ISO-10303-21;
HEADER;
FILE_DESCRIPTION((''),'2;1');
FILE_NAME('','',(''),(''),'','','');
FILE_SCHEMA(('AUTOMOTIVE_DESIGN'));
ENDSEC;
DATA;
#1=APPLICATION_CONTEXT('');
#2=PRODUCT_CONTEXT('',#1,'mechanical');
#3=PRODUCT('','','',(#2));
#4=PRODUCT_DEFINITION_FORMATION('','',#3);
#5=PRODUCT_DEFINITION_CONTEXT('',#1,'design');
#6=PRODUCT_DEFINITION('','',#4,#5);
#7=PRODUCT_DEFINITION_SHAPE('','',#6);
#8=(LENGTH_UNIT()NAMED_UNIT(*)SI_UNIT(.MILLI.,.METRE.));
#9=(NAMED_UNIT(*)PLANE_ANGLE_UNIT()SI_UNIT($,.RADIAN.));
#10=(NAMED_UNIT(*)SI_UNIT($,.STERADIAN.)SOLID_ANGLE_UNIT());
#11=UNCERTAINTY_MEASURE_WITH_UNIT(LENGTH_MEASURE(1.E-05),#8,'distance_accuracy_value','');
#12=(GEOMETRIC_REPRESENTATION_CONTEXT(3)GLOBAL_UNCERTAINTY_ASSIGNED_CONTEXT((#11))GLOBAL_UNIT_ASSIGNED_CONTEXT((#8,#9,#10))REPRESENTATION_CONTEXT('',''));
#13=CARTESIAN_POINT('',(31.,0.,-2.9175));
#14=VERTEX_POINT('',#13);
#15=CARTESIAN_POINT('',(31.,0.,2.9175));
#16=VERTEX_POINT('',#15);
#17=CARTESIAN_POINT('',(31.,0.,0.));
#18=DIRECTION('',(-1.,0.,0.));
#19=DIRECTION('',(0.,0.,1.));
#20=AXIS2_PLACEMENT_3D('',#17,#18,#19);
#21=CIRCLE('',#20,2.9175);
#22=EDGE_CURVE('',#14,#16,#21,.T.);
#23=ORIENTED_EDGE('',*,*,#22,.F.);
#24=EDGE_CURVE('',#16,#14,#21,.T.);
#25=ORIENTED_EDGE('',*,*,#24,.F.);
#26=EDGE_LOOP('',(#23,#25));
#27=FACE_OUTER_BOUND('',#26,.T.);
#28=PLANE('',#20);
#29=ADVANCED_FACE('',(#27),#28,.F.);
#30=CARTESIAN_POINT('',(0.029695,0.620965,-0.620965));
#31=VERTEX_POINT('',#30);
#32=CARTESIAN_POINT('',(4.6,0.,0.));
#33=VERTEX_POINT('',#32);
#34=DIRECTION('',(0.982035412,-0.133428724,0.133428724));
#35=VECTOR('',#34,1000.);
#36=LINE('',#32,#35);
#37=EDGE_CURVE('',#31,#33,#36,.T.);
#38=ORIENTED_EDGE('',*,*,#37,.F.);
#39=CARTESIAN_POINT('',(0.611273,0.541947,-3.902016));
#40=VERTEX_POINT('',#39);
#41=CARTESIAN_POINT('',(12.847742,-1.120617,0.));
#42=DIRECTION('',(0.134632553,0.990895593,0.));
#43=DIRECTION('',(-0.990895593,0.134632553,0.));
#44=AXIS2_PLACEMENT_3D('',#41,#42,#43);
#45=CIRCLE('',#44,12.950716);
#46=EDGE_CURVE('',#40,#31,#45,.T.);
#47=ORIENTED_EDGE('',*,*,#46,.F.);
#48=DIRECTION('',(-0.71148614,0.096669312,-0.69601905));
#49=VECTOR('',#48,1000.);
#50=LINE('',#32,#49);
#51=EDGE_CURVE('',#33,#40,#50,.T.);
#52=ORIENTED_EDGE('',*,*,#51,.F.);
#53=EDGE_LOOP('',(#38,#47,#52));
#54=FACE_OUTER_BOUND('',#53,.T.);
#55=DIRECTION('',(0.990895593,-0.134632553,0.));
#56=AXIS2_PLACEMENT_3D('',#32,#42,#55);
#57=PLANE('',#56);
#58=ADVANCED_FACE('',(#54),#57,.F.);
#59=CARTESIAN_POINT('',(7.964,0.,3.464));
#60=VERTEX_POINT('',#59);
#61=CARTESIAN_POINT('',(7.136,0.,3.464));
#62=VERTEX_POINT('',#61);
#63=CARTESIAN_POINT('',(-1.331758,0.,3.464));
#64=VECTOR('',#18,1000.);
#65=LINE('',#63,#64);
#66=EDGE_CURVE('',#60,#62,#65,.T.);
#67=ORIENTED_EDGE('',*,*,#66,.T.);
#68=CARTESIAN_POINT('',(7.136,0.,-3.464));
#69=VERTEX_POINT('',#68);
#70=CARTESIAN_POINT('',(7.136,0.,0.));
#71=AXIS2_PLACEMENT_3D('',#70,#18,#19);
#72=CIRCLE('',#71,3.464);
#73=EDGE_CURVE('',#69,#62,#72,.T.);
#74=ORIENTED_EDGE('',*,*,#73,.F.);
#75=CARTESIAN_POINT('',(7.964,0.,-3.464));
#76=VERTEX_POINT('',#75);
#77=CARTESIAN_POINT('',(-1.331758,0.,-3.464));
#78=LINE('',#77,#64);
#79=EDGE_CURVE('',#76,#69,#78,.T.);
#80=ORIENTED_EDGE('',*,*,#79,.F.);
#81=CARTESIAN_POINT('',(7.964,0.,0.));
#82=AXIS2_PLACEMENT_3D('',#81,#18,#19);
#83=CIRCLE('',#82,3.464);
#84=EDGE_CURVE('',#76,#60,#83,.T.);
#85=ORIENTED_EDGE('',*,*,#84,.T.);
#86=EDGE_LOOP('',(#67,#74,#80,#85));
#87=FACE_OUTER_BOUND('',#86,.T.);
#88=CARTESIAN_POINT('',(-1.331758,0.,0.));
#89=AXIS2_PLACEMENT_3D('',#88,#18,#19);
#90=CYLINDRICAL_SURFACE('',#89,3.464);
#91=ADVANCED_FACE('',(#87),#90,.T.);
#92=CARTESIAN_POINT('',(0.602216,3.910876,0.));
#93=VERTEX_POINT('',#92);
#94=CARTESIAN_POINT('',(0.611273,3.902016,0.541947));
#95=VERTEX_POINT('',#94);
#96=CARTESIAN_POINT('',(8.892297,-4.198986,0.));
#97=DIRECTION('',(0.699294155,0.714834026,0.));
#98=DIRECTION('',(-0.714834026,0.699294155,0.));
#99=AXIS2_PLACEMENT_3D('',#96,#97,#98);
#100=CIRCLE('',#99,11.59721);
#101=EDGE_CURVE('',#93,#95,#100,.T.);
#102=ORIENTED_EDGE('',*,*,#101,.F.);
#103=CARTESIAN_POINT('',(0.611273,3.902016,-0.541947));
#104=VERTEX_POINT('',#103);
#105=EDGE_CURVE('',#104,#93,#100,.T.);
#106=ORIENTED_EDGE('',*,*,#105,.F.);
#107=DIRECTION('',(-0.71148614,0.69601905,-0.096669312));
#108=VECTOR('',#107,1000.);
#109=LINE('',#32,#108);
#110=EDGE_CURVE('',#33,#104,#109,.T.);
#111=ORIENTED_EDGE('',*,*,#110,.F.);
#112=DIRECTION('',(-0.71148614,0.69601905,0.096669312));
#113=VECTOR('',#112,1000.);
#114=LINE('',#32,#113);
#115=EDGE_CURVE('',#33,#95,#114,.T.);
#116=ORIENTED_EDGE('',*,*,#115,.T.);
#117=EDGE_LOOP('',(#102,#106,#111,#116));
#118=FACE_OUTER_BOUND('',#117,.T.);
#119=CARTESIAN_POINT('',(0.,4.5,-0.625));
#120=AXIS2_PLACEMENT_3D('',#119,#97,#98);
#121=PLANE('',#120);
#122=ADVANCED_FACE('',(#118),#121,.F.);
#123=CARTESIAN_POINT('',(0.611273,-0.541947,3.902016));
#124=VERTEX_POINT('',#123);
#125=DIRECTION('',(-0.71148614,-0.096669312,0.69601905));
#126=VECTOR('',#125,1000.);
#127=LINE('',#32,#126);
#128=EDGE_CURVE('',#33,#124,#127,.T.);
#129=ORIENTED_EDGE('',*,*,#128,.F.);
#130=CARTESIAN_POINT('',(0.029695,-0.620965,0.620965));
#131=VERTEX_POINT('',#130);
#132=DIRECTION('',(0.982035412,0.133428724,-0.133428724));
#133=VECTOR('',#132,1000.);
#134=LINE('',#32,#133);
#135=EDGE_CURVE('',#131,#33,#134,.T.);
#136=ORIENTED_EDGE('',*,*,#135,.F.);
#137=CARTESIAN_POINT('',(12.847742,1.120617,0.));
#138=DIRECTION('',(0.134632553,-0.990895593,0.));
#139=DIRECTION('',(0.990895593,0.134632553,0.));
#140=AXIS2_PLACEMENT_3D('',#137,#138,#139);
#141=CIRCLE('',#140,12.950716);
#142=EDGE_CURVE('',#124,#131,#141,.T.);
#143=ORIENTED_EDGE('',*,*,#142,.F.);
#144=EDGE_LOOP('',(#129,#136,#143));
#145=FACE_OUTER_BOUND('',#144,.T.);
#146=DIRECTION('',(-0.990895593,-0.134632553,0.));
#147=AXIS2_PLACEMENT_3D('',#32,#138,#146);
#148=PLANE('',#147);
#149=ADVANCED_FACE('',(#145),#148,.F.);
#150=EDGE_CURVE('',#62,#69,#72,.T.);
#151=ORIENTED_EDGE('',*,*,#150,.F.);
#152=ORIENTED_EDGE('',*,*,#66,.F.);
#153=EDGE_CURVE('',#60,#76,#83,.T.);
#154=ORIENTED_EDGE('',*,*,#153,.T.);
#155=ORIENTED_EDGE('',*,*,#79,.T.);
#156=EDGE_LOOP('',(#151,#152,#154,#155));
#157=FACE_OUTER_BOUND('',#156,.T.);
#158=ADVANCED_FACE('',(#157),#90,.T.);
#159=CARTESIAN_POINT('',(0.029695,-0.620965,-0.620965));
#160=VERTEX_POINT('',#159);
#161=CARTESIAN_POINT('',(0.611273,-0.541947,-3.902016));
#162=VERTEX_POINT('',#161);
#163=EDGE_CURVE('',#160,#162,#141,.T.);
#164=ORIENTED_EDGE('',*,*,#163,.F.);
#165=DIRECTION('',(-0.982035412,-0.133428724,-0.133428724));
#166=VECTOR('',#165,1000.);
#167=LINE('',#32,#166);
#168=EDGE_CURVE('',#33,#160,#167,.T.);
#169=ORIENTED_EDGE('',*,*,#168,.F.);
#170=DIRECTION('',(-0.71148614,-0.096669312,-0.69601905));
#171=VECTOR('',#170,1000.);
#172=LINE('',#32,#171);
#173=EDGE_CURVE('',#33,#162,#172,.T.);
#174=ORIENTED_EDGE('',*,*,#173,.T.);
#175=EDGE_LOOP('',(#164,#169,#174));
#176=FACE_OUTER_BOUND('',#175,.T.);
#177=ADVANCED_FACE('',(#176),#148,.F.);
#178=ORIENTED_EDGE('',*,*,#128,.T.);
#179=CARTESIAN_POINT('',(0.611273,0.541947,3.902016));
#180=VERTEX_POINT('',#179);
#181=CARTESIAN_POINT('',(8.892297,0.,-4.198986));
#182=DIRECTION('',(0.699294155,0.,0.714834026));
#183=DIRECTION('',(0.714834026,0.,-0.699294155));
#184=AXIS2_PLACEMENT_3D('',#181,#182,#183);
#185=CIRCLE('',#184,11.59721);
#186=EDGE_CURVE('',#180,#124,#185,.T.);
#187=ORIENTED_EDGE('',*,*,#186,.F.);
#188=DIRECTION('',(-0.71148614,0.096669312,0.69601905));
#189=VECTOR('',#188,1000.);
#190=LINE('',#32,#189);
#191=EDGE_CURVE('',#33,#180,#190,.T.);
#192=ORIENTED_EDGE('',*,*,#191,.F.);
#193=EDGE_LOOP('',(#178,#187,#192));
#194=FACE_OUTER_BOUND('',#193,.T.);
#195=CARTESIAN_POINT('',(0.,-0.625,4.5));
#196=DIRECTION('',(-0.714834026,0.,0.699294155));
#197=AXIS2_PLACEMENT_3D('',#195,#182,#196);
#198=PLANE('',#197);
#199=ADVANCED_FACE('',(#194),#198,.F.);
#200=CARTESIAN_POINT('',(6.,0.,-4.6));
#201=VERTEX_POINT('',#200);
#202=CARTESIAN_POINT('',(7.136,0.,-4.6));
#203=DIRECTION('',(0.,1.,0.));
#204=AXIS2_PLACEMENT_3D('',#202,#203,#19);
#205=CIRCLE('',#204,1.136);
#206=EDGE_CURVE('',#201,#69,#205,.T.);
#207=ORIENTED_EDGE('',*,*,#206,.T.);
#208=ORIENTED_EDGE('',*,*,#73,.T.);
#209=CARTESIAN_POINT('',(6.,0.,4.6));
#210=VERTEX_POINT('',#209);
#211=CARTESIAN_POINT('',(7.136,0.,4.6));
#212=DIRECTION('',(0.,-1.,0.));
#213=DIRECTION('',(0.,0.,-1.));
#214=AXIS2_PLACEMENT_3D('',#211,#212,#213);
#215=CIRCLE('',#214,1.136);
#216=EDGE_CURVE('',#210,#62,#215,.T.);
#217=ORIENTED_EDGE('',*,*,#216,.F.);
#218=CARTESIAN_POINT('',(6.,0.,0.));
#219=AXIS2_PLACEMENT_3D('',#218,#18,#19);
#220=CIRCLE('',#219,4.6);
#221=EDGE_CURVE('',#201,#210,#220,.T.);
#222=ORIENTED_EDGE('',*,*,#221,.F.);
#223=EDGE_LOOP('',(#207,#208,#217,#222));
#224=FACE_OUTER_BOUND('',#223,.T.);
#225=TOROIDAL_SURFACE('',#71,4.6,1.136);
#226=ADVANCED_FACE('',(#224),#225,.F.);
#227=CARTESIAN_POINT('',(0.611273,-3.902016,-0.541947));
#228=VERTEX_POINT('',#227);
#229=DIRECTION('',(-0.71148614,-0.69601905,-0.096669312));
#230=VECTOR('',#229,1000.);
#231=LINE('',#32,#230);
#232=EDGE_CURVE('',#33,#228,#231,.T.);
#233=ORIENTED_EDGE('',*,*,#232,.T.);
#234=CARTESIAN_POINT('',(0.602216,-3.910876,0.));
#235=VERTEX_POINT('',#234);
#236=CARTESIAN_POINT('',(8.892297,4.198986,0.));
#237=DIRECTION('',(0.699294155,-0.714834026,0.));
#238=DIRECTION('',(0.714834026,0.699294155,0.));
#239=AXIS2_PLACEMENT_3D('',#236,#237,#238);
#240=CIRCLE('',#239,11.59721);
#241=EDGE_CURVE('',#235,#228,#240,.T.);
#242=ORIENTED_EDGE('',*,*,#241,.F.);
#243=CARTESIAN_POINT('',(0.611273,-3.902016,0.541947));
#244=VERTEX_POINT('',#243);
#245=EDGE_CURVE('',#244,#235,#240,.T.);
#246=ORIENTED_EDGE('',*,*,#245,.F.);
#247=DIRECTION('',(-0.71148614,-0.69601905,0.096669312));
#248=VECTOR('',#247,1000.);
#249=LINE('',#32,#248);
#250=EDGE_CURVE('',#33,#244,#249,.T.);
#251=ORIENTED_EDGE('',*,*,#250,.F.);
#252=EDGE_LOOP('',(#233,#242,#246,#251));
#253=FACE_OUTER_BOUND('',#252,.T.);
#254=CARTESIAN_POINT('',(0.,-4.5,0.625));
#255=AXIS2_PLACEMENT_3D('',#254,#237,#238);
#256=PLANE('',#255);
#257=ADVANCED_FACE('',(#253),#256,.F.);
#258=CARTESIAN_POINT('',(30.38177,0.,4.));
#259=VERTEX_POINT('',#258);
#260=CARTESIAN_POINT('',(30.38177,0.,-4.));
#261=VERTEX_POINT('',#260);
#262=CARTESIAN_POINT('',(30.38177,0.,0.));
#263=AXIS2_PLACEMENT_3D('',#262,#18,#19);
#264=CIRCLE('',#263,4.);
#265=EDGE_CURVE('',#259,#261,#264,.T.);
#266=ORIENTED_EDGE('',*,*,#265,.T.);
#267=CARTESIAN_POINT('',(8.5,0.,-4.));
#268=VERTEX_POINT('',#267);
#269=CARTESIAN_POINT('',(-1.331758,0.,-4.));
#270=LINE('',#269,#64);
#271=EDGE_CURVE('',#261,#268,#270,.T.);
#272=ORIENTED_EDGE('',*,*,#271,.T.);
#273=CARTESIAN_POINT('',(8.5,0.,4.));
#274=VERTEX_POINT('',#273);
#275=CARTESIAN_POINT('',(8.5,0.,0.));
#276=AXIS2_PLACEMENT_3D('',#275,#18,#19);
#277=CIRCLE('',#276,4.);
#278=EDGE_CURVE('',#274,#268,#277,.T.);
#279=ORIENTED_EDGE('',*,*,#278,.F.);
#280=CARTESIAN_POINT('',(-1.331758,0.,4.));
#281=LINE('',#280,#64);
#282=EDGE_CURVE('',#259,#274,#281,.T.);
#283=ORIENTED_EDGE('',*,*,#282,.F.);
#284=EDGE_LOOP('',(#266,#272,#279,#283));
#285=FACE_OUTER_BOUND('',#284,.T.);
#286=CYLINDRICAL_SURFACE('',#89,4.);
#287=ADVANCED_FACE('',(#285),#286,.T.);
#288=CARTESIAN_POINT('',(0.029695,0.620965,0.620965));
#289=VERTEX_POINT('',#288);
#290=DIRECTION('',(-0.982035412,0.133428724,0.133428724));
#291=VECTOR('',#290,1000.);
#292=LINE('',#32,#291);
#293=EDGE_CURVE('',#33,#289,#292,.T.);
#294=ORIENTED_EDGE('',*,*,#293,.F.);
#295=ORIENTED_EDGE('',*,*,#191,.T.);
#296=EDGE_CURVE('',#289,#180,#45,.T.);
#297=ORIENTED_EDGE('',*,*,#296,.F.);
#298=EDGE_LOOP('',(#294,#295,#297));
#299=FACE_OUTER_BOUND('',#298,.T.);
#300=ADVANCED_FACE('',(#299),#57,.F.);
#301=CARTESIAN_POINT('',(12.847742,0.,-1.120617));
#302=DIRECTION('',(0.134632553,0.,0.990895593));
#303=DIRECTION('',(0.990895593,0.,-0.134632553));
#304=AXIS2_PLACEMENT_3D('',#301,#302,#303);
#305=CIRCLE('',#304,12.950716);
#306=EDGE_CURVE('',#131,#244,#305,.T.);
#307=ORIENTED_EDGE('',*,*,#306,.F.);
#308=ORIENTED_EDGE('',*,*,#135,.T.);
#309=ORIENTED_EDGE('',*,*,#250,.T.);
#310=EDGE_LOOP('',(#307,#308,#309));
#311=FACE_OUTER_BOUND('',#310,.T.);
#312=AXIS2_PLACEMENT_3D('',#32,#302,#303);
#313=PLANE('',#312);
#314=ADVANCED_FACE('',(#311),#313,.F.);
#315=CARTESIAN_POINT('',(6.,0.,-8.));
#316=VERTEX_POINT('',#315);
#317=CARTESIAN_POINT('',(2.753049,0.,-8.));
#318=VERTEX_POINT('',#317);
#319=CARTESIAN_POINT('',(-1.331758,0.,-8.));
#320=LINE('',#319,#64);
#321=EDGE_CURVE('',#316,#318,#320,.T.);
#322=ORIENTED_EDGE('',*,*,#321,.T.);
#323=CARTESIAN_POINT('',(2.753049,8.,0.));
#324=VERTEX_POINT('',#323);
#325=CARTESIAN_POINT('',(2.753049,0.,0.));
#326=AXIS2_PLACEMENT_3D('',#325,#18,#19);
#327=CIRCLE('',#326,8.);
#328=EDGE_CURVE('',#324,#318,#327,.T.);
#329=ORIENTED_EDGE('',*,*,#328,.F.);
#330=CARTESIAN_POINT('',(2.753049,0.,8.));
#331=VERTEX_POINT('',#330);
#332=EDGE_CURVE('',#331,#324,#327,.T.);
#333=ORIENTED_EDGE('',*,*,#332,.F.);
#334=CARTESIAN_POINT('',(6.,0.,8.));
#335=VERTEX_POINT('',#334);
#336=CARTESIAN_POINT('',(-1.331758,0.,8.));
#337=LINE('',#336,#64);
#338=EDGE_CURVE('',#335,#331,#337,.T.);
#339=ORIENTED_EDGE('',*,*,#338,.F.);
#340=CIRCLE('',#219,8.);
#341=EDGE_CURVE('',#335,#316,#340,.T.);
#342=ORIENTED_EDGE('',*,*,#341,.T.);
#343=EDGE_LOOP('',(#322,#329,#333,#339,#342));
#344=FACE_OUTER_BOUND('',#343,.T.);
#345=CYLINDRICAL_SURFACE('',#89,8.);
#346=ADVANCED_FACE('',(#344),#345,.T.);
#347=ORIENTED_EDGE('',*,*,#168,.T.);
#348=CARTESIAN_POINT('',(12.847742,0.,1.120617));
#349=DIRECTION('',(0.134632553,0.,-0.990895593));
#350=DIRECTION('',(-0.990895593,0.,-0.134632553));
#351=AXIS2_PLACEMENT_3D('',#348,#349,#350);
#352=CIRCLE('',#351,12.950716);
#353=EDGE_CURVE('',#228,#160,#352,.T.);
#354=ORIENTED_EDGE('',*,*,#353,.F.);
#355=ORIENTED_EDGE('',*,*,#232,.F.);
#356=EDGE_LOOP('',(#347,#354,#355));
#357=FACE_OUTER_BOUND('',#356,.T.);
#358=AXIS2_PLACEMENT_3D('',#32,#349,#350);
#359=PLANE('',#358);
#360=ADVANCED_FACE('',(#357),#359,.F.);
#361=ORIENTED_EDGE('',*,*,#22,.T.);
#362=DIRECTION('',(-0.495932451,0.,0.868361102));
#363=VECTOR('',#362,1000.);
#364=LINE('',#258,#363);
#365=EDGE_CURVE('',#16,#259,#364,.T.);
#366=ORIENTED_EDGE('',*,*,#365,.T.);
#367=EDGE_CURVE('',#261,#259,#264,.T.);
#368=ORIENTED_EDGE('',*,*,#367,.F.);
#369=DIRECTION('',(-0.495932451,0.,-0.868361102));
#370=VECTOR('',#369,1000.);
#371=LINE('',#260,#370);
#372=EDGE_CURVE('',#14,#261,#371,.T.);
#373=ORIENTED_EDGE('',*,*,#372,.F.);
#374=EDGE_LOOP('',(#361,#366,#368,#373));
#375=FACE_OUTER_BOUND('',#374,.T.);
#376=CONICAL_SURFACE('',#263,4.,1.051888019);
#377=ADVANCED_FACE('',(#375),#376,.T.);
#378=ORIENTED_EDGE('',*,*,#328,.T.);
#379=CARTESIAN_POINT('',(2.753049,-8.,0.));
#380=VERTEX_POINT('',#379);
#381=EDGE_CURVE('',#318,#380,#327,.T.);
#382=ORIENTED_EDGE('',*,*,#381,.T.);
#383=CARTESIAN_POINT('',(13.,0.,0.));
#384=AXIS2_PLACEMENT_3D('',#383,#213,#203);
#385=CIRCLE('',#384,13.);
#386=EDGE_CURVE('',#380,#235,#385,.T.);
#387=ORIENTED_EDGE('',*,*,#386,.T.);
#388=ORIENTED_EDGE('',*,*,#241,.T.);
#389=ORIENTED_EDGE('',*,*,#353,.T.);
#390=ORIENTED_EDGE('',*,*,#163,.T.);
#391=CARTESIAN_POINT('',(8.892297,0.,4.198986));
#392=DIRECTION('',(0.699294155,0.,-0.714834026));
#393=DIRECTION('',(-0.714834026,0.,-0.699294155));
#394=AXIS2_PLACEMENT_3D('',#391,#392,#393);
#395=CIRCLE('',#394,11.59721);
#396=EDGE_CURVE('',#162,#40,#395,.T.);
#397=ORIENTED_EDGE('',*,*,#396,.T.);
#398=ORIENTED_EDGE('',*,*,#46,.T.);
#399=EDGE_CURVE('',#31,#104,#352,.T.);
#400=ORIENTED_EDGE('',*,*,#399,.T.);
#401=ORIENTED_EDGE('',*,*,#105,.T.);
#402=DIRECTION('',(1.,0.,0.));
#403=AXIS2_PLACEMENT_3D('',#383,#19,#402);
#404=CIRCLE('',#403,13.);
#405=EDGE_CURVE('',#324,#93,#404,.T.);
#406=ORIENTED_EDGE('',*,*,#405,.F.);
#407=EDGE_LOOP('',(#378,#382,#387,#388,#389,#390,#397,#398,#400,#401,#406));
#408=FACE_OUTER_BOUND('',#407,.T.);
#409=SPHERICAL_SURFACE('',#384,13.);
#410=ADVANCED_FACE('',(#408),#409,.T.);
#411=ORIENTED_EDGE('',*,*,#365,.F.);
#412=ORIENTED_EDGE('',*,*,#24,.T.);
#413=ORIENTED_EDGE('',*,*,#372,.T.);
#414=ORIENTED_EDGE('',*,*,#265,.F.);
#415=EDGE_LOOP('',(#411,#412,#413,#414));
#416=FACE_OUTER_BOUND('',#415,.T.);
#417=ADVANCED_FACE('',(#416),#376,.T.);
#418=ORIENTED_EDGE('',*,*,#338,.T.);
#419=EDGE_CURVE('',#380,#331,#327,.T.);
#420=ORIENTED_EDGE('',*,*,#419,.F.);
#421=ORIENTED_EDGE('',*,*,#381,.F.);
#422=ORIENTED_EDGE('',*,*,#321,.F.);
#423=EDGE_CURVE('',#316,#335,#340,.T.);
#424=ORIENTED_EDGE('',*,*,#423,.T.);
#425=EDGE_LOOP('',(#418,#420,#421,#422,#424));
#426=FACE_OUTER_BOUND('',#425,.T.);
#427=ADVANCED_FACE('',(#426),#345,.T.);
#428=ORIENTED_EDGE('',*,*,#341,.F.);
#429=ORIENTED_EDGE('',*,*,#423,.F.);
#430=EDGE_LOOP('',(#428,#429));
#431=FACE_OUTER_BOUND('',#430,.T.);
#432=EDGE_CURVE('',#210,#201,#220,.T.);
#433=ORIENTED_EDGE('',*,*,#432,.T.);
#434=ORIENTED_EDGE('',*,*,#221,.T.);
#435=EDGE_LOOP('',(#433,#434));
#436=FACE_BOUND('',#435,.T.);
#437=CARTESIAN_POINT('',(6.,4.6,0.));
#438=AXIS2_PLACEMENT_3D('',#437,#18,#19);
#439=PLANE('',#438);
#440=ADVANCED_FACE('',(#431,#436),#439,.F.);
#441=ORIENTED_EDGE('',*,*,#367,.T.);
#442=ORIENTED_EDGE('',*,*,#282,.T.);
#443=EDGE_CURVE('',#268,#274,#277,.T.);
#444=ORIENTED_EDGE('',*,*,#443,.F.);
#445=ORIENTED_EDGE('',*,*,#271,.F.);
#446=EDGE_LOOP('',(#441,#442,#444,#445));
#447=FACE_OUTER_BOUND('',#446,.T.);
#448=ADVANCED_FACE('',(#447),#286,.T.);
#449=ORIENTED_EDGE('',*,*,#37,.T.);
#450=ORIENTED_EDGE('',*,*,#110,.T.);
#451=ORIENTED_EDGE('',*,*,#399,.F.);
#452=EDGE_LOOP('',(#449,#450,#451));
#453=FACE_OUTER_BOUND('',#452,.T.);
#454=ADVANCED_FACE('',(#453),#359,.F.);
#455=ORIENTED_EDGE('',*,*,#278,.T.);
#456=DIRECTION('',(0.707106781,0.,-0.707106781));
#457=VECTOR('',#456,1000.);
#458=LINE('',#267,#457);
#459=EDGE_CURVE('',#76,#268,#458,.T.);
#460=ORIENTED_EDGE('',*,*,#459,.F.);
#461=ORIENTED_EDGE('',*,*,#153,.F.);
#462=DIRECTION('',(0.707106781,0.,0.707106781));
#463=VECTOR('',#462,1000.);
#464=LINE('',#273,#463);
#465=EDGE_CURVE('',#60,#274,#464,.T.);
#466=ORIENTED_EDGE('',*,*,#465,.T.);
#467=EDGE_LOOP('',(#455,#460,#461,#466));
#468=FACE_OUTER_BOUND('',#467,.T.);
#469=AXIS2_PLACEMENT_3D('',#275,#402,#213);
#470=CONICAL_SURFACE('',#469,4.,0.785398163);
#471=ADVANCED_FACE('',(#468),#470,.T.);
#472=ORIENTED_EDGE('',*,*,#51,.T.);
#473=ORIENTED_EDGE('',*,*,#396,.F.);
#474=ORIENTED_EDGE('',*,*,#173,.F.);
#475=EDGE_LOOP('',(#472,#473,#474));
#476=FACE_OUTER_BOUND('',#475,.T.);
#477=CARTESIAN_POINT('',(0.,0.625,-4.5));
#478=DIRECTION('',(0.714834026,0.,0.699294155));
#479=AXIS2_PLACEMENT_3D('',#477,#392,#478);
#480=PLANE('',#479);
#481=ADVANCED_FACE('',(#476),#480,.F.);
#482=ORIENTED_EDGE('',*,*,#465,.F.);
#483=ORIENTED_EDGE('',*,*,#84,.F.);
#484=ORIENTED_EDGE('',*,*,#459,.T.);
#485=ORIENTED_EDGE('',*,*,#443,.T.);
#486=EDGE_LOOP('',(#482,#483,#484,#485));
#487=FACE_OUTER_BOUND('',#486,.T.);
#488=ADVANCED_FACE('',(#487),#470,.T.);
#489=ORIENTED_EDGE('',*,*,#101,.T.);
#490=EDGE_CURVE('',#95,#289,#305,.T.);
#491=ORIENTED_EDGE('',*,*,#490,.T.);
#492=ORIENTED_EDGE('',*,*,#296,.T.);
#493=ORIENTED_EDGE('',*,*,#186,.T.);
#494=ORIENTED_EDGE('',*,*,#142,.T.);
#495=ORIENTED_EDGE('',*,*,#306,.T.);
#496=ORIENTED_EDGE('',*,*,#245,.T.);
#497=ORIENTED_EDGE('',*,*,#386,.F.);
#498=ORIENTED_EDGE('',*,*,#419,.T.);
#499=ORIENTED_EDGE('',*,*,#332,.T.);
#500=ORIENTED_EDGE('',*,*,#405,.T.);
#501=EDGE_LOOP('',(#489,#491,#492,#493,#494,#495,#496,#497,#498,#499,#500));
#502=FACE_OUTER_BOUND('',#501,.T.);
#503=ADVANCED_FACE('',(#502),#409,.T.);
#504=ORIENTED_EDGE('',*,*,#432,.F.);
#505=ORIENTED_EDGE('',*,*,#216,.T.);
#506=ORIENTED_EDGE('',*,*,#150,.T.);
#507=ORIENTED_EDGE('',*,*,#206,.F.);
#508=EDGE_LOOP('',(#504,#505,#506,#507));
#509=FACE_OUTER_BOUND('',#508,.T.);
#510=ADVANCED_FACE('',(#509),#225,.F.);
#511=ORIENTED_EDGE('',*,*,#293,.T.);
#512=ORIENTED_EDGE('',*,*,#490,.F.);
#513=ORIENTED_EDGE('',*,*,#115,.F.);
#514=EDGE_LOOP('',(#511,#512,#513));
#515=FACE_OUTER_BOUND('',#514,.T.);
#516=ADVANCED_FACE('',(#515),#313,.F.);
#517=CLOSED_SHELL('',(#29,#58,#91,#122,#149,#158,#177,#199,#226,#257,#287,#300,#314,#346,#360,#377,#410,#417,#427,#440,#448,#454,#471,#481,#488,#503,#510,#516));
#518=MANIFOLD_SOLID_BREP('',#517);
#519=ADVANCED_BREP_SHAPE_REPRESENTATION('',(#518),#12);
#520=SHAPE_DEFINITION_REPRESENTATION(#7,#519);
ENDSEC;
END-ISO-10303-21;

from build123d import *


with BuildPart() as part:
    # 草图2 → Revolve 709 (revolve)
    with BuildSketch(Plane.XY, mode=Mode.PRIVATE) as revolve_709_sk:
        with BuildLine():
            Line((0, 0), (31, 0))
            Line((31, 0), (31, 4))
            Line((31, 4), (8.5, 4))
            Line((8.5, 4), (7.964, 3.464))
            Line((7.964, 3.464), (7.136, 3.464))
            ThreePointArc((7.136, 3.464), (6.332726697, 3.796726697), (6, 4.6))
            Line((6, 4.6), (6, 8))
            Line((6, 8), (2.753049234, 8))
            ThreePointArc((2.753049234, 8), (0.707515305, 4.230226947), (0, 0))
        make_face()
    revolve(revolve_709_sk.sketch.rotate(Axis((-1.331757704, 0, 0), (1, 0, 0)), 90), axis=Axis((-1.331757704, 0, 0), (1, 0, 0)))

    # 草图3 → 切除-旋转1 (revolve, cut)
    with BuildSketch(Plane.XY, mode=Mode.PRIVATE) as cut_revolve_1_sk:
        Polygon((30.381770007, 4), (31.631770007, 4), (31, 2.9175), align=None)
    revolve(cut_revolve_1_sk.sketch.rotate(Axis((-0.242766179, 0, 0), (1, 0, 0)), 90), axis=Axis((-0.242766179, 0, 0), (1, 0, 0)), mode=Mode.SUBTRACT)

    # 草图5 → 切除-放样1 section 0
    with BuildSketch(Plane(origin=(0, 0, 0), x_dir=(0, 0, -1), z_dir=(1, 0, 0)), mode=Mode.PRIVATE) as loft_1_s0:
        with BuildLine():
            Line((0.625, 4.5), (-0.625, 4.5))
            Line((-0.625, 4.5), (-0.625, -4.5))
            Line((-0.625, -4.5), (0.625, -4.5))
            Line((0.625, -4.5), (0.625, 4.5))
        make_face()
    loft_1 = loft([Vertex(4.6, 0, 0), loft_1_s0.sketch], mode=Mode.SUBTRACT)

    # 镜向1: 切除-放样1 across plane
    add(loft_1.mirror(Plane(origin=(0, 0, 0), x_dir=(0, 0.7071067811865462, 0.7071067811865488), z_dir=(0, -0.7071067811865488, 0.7071067811865462))), mode=Mode.SUBTRACT)


solid = part.part
